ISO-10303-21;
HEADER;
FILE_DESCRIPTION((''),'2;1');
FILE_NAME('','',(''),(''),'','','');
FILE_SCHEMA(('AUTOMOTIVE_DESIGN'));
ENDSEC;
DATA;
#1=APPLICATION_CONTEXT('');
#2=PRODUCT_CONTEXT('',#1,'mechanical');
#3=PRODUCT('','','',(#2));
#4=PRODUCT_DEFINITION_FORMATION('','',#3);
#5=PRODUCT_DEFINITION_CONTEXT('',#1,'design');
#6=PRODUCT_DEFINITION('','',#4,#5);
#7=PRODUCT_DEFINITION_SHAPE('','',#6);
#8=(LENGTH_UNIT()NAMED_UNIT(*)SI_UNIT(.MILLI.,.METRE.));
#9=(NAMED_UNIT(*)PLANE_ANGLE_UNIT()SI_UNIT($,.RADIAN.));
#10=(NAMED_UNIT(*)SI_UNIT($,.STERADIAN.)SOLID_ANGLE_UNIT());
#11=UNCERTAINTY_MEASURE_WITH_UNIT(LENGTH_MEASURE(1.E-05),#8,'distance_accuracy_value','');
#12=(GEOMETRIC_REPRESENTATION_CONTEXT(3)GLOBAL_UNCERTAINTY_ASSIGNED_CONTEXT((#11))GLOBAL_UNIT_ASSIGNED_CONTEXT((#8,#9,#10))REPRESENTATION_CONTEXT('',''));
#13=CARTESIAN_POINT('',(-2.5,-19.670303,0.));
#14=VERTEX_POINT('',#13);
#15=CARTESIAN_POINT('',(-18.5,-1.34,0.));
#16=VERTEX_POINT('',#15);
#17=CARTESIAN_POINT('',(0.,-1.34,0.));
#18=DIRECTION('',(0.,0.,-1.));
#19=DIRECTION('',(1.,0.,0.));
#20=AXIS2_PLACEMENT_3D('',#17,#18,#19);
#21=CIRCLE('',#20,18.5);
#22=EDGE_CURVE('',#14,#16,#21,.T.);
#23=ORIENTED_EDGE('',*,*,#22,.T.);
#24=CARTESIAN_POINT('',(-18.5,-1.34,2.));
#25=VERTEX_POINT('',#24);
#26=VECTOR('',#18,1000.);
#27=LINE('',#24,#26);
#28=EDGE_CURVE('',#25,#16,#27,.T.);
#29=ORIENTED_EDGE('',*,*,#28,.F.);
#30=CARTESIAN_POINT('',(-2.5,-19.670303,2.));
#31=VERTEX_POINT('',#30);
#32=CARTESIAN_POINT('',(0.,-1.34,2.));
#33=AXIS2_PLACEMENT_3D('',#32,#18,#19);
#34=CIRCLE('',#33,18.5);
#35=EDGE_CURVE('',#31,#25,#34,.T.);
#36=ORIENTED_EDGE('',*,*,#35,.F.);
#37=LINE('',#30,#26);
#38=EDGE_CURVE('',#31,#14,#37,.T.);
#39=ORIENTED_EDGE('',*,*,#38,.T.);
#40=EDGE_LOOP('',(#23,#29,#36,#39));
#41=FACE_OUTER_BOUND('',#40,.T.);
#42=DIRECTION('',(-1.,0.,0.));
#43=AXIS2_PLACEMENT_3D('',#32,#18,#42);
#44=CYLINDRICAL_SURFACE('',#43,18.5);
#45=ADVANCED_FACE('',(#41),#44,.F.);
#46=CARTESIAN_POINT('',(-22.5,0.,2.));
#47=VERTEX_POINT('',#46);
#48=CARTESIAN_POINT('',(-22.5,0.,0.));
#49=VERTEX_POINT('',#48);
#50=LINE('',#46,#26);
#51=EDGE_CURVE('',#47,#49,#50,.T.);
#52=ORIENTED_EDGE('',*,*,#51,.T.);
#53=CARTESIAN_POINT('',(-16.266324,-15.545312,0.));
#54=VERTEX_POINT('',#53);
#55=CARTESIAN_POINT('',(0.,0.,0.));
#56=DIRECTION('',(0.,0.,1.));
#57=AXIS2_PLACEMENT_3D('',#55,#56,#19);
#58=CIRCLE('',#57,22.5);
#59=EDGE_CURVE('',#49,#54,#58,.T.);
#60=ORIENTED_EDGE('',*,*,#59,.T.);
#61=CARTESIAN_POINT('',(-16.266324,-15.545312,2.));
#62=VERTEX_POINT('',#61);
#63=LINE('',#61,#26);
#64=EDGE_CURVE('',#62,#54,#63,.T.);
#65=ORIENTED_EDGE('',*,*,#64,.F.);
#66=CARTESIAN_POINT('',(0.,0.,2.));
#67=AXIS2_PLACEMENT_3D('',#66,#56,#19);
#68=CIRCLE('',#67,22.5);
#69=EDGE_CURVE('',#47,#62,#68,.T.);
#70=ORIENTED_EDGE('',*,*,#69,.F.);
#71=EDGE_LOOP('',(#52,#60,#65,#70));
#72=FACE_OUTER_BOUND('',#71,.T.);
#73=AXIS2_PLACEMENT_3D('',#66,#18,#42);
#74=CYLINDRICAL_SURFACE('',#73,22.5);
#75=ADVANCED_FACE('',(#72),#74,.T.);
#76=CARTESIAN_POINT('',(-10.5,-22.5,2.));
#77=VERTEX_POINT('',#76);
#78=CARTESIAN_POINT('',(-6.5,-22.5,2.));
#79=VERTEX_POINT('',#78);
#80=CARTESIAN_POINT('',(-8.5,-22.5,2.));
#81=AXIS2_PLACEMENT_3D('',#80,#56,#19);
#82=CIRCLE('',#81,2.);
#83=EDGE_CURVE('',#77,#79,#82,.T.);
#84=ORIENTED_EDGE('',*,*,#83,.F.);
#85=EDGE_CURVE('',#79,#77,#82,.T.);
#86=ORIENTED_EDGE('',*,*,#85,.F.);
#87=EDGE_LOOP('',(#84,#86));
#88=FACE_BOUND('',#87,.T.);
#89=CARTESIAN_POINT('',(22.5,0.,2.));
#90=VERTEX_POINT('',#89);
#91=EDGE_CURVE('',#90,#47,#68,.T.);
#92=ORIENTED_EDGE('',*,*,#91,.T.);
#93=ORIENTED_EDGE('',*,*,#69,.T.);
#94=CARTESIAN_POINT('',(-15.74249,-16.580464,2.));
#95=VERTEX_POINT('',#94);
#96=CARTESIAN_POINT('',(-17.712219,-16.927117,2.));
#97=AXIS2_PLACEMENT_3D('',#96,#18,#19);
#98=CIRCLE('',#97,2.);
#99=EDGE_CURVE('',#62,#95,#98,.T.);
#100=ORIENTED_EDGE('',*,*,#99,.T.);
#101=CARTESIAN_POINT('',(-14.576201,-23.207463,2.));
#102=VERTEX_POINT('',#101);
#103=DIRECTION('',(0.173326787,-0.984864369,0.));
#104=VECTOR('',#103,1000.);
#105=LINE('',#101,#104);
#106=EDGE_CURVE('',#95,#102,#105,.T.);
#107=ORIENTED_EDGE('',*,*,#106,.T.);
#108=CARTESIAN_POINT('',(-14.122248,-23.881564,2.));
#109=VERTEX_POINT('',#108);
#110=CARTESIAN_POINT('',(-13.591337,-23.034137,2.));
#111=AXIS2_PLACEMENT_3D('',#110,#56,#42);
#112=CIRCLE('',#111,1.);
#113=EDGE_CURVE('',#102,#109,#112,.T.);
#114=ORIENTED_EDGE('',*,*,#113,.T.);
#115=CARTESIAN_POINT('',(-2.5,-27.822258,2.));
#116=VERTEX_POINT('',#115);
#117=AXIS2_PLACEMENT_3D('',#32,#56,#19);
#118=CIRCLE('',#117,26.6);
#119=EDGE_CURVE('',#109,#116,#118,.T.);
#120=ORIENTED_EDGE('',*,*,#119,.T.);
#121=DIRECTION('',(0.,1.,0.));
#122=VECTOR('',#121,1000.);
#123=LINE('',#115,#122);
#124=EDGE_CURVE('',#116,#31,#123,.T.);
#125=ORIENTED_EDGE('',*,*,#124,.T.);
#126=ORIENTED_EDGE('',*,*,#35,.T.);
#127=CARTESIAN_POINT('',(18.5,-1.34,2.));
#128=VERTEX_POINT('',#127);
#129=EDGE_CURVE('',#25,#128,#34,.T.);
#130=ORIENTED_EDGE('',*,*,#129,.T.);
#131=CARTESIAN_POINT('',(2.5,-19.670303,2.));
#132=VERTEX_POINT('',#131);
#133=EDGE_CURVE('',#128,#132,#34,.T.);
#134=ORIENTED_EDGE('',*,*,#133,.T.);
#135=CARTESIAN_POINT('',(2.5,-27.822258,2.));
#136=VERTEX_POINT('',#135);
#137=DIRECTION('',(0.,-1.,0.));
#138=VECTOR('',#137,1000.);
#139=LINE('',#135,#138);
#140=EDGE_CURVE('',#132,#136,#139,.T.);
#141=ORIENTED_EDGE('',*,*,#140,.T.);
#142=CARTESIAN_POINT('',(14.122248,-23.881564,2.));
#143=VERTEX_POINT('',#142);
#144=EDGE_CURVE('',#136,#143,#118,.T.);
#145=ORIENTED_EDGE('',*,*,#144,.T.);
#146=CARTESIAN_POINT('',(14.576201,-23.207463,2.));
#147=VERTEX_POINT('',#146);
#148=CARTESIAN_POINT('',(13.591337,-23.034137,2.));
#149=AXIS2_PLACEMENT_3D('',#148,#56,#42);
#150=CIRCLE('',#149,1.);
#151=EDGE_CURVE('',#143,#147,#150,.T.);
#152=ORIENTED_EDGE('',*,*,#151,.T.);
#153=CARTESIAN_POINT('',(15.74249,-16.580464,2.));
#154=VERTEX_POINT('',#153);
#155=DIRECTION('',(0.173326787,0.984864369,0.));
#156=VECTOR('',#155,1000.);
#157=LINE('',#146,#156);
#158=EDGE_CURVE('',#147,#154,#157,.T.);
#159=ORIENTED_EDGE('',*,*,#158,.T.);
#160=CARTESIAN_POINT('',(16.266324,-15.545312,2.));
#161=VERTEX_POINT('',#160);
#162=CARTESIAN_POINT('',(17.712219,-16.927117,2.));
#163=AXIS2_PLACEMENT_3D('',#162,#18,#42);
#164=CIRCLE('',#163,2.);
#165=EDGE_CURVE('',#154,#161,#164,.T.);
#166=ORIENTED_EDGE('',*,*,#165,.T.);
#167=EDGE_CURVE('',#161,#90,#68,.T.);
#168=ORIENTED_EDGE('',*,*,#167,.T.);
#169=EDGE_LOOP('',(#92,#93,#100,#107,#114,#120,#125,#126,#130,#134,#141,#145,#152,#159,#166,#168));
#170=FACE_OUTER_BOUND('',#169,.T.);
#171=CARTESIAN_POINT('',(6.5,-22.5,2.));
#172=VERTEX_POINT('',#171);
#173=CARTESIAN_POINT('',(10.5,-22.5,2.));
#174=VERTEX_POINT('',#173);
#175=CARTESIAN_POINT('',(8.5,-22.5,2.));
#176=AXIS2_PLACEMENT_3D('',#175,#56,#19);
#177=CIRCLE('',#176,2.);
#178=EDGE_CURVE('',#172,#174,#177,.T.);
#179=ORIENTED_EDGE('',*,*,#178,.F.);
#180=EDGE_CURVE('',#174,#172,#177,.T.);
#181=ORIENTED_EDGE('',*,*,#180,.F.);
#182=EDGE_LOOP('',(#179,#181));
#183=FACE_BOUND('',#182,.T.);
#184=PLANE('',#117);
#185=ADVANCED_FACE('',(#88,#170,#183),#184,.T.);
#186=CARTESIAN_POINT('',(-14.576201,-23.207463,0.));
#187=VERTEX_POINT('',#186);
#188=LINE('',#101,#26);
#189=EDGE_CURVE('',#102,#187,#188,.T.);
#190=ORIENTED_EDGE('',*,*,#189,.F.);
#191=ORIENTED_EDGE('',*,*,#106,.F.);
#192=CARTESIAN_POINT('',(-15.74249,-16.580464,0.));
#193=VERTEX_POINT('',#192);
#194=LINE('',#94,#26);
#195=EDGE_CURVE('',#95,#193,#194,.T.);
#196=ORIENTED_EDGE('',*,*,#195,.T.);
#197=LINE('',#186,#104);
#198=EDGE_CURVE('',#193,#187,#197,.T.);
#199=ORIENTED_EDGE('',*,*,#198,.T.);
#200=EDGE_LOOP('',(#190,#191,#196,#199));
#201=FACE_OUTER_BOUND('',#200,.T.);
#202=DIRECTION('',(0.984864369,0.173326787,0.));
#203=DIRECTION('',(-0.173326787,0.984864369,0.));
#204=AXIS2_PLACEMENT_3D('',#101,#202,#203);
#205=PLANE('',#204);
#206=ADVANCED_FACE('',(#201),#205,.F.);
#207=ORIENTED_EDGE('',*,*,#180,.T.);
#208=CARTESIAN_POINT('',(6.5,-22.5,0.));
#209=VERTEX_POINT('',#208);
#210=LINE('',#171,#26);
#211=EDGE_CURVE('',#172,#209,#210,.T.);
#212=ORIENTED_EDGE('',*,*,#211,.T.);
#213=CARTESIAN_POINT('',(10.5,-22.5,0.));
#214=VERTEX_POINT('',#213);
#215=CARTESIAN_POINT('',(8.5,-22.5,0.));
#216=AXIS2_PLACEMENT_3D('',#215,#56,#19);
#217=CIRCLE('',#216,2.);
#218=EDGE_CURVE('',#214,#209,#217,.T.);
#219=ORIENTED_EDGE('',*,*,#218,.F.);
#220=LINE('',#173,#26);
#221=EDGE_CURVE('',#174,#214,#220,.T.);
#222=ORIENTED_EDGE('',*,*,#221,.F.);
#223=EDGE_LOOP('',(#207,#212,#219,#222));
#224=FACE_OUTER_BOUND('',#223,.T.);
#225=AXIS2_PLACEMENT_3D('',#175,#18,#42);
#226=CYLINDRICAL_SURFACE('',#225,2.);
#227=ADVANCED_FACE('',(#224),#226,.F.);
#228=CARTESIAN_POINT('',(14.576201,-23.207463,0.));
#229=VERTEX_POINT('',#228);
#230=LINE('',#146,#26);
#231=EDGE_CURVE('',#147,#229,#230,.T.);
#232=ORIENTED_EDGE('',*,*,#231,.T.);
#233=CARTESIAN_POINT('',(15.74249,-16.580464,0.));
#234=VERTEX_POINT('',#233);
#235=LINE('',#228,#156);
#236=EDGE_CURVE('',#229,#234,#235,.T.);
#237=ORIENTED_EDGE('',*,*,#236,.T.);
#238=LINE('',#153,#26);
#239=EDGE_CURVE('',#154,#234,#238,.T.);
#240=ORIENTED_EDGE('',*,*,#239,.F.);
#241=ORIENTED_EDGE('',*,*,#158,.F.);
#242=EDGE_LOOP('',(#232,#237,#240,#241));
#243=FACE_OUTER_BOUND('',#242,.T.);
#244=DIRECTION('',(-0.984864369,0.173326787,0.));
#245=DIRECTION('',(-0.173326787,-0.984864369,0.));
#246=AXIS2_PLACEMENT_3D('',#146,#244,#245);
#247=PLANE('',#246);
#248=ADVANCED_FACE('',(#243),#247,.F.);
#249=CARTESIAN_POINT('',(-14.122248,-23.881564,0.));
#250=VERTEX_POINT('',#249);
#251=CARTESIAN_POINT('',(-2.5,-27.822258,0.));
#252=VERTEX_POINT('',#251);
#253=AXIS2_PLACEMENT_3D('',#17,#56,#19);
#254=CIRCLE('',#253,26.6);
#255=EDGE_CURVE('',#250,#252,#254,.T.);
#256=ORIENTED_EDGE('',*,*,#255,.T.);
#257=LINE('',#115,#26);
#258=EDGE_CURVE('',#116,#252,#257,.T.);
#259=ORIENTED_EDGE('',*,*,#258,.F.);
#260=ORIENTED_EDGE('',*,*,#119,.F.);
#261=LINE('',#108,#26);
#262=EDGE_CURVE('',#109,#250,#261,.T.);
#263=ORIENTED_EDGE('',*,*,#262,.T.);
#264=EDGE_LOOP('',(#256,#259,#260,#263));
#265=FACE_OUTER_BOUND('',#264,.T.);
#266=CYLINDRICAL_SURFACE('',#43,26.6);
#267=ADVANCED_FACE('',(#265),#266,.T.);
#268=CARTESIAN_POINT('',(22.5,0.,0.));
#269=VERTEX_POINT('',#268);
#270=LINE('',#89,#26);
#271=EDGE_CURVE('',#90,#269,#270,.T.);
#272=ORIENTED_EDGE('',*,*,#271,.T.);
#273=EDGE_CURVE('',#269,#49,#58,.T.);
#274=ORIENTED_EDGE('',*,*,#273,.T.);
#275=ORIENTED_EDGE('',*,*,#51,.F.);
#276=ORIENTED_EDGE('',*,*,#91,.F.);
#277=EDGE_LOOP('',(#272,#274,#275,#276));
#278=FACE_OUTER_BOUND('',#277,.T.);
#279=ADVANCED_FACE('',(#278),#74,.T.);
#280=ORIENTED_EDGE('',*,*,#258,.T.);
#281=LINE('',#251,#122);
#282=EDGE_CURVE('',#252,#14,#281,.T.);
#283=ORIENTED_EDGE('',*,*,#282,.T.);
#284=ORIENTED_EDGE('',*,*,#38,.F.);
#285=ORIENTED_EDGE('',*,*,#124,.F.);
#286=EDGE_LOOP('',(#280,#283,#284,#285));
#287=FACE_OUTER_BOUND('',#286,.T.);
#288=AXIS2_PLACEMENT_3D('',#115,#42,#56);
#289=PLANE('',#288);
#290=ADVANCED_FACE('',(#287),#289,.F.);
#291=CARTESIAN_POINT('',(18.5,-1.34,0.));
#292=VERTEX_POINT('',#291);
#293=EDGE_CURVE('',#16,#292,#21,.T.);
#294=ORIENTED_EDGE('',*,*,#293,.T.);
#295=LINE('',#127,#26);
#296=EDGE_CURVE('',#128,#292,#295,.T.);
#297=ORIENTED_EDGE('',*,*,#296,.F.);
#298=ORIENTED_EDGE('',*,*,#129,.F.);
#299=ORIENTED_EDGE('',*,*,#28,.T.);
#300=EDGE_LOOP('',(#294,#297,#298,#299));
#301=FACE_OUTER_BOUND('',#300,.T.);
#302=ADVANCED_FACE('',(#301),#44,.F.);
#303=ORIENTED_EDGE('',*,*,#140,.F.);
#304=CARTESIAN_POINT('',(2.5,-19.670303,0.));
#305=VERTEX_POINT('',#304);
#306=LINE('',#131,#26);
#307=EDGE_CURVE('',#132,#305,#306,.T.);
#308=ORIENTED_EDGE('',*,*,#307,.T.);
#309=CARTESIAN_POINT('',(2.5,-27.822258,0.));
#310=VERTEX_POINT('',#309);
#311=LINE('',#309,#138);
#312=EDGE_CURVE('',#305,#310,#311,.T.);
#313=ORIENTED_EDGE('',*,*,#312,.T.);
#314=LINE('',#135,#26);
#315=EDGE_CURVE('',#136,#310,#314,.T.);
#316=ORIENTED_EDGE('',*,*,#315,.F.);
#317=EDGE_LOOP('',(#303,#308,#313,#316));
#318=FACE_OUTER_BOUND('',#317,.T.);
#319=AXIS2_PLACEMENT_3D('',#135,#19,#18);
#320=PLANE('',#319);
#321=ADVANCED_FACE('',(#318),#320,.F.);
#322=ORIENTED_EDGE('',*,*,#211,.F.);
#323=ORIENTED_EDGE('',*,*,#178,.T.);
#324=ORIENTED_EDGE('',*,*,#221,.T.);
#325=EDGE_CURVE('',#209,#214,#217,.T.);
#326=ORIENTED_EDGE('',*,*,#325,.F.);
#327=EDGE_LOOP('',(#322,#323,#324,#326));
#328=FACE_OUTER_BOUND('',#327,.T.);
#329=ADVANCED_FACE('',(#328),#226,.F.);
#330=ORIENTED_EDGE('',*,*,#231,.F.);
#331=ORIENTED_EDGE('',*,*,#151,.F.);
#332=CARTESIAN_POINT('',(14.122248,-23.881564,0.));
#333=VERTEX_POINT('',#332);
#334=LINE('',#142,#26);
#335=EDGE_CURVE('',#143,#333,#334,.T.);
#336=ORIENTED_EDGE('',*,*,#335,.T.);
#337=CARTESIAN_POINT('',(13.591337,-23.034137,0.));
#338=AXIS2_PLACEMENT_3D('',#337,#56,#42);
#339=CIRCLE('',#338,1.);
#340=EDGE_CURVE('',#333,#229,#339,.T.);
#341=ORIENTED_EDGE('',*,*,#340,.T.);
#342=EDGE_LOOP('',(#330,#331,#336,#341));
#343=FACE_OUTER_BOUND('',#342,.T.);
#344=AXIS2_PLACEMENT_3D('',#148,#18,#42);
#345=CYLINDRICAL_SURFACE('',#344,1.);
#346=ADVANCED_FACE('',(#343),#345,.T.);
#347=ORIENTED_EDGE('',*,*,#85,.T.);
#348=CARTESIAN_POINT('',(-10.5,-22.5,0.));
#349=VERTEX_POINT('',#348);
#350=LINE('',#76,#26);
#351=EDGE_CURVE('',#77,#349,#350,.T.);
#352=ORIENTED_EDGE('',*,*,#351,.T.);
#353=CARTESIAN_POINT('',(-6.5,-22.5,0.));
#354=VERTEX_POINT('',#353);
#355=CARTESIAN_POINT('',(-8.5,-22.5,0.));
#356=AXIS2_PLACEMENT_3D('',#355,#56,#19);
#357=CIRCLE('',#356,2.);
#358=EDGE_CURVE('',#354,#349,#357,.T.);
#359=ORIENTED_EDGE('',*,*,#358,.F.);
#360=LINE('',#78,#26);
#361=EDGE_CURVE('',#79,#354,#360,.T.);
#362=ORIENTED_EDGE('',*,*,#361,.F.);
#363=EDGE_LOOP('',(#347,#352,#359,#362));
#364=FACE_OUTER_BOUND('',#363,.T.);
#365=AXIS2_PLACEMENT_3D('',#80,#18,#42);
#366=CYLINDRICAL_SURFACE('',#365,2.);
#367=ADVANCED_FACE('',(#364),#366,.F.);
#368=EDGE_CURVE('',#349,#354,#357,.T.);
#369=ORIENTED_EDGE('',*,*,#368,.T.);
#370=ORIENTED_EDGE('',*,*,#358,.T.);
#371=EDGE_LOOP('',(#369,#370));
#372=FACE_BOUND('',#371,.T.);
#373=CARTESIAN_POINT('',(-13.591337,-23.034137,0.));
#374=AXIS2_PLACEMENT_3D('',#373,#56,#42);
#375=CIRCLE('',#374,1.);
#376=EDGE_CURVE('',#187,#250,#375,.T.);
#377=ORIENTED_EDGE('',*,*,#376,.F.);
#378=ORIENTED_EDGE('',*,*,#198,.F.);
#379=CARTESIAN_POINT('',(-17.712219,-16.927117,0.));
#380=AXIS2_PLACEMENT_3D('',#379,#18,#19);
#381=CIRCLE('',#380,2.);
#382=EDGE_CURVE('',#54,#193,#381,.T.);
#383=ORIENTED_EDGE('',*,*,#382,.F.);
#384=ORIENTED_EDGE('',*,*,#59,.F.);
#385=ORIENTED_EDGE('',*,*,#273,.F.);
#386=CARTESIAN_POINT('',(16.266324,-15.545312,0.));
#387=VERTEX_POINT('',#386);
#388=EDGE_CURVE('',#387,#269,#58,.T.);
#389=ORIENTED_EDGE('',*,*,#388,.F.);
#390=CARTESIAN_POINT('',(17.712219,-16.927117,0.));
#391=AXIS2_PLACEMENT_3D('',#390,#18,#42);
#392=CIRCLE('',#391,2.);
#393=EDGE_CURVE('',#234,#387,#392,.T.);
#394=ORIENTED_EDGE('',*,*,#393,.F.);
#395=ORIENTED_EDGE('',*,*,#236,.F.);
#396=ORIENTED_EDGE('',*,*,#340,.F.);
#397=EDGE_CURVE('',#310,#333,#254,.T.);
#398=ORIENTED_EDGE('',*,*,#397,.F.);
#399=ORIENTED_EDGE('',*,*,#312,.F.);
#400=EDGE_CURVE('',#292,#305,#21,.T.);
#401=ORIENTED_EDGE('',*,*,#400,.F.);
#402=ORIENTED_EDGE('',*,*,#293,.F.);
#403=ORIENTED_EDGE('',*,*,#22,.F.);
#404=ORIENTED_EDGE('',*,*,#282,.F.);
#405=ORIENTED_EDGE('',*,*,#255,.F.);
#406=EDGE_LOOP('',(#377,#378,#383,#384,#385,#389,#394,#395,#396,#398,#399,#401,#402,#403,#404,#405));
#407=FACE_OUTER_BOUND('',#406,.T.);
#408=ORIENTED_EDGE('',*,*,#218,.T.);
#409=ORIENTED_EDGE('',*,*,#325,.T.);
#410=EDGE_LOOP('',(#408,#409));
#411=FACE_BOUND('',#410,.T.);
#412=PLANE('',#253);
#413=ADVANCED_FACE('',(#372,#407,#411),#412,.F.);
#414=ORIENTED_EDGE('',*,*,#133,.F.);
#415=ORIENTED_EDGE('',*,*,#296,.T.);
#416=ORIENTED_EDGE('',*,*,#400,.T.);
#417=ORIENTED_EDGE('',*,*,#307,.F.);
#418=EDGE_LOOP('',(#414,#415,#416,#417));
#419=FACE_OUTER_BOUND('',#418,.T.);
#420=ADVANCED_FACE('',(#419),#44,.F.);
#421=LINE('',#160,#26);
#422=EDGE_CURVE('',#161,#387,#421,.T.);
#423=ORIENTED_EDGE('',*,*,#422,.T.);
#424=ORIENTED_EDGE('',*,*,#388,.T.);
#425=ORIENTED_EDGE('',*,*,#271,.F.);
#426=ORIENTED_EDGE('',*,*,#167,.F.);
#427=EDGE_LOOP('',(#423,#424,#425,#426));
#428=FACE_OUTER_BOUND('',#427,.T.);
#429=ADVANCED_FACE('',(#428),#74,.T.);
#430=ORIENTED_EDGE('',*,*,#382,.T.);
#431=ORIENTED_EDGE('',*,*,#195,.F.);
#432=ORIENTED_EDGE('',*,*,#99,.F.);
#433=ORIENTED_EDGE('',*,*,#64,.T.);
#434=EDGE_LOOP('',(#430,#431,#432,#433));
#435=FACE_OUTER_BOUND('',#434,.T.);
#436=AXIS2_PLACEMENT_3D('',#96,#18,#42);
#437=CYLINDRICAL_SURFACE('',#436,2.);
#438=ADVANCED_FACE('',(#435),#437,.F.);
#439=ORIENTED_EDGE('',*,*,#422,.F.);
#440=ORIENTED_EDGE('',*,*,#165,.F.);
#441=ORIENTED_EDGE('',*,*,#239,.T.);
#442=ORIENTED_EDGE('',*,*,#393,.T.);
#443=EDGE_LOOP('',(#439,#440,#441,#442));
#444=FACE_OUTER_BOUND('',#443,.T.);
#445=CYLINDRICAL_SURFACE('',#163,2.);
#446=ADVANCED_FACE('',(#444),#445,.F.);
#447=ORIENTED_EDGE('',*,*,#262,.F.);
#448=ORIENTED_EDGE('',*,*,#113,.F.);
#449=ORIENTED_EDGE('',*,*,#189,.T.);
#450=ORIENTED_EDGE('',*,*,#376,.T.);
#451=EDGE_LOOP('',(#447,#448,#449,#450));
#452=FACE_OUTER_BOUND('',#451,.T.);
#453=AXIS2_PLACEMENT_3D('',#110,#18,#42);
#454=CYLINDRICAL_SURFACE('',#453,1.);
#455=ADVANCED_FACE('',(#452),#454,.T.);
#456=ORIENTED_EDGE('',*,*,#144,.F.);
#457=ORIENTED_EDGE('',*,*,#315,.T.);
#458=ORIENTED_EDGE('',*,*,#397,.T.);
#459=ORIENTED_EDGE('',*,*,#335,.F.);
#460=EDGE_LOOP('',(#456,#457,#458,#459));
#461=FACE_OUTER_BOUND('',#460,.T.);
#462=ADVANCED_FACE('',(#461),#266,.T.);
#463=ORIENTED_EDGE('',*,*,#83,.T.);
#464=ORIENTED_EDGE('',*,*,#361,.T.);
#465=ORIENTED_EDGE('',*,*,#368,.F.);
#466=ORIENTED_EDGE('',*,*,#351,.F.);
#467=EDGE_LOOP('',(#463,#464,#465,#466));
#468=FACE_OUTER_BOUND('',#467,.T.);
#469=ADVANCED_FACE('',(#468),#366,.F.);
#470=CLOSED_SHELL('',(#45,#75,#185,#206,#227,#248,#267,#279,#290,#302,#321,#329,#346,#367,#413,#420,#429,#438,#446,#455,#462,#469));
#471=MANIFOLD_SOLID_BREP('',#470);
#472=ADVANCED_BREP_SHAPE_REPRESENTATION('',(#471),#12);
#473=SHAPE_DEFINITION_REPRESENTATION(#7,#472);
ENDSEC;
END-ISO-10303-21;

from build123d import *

# Parameters (mm, degrees)
SKETCH_1_R      = 2
EXTRUDE_1_DEPTH = 2


with BuildPart() as part:
    # 草图1 → 凸台-拉伸1 (new body)
    with BuildSketch(Plane.XY):
        with BuildLine():
            Line((-14.576201266, -23.207463353), (-15.742490369, -16.580463555))
            ThreePointArc((-15.742490369, -16.580463555), (-15.927700406, -16.024070615), (-16.26632367, -15.545311649))
            ThreePointArc((-16.26632367, -15.545311649), (0, 22.5), (16.26632367, -15.545311649))
            ThreePointArc((16.26632367, -15.545311649), (15.927700406, -16.024070615), (15.742490369, -16.580463555))
            Line((15.742490369, -16.580463555), (14.576201266, -23.207463353))
            ThreePointArc((14.576201266, -23.207463353), (14.420792767, -23.592708818), (14.122248494, -23.881563776))
            ThreePointArc((14.122248494, -23.881563776), (8.541490175, -26.531326793), (2.5, -27.822258212))
            Line((2.5, -27.822258212), (2.5, -19.67030278))
            ThreePointArc((2.5, -19.67030278), (0, 17.16), (-2.5, -19.67030278))
            Line((-2.5, -19.67030278), (-2.5, -27.822258212))
            ThreePointArc((-2.5, -27.822258212), (-8.541490175, -26.531326793), (-14.122248494, -23.881563776))
            ThreePointArc((-14.122248494, -23.881563776), (-14.420792767, -23.592708818), (-14.576201266, -23.207463353))
        make_face()
        with Locations((-8.5, -22.5)):
            Circle(SKETCH_1_R, mode=Mode.SUBTRACT)
        with Locations((8.5, -22.5)):
            Circle(SKETCH_1_R, mode=Mode.SUBTRACT)
    extrude(amount=EXTRUDE_1_DEPTH)


solid = part.part
